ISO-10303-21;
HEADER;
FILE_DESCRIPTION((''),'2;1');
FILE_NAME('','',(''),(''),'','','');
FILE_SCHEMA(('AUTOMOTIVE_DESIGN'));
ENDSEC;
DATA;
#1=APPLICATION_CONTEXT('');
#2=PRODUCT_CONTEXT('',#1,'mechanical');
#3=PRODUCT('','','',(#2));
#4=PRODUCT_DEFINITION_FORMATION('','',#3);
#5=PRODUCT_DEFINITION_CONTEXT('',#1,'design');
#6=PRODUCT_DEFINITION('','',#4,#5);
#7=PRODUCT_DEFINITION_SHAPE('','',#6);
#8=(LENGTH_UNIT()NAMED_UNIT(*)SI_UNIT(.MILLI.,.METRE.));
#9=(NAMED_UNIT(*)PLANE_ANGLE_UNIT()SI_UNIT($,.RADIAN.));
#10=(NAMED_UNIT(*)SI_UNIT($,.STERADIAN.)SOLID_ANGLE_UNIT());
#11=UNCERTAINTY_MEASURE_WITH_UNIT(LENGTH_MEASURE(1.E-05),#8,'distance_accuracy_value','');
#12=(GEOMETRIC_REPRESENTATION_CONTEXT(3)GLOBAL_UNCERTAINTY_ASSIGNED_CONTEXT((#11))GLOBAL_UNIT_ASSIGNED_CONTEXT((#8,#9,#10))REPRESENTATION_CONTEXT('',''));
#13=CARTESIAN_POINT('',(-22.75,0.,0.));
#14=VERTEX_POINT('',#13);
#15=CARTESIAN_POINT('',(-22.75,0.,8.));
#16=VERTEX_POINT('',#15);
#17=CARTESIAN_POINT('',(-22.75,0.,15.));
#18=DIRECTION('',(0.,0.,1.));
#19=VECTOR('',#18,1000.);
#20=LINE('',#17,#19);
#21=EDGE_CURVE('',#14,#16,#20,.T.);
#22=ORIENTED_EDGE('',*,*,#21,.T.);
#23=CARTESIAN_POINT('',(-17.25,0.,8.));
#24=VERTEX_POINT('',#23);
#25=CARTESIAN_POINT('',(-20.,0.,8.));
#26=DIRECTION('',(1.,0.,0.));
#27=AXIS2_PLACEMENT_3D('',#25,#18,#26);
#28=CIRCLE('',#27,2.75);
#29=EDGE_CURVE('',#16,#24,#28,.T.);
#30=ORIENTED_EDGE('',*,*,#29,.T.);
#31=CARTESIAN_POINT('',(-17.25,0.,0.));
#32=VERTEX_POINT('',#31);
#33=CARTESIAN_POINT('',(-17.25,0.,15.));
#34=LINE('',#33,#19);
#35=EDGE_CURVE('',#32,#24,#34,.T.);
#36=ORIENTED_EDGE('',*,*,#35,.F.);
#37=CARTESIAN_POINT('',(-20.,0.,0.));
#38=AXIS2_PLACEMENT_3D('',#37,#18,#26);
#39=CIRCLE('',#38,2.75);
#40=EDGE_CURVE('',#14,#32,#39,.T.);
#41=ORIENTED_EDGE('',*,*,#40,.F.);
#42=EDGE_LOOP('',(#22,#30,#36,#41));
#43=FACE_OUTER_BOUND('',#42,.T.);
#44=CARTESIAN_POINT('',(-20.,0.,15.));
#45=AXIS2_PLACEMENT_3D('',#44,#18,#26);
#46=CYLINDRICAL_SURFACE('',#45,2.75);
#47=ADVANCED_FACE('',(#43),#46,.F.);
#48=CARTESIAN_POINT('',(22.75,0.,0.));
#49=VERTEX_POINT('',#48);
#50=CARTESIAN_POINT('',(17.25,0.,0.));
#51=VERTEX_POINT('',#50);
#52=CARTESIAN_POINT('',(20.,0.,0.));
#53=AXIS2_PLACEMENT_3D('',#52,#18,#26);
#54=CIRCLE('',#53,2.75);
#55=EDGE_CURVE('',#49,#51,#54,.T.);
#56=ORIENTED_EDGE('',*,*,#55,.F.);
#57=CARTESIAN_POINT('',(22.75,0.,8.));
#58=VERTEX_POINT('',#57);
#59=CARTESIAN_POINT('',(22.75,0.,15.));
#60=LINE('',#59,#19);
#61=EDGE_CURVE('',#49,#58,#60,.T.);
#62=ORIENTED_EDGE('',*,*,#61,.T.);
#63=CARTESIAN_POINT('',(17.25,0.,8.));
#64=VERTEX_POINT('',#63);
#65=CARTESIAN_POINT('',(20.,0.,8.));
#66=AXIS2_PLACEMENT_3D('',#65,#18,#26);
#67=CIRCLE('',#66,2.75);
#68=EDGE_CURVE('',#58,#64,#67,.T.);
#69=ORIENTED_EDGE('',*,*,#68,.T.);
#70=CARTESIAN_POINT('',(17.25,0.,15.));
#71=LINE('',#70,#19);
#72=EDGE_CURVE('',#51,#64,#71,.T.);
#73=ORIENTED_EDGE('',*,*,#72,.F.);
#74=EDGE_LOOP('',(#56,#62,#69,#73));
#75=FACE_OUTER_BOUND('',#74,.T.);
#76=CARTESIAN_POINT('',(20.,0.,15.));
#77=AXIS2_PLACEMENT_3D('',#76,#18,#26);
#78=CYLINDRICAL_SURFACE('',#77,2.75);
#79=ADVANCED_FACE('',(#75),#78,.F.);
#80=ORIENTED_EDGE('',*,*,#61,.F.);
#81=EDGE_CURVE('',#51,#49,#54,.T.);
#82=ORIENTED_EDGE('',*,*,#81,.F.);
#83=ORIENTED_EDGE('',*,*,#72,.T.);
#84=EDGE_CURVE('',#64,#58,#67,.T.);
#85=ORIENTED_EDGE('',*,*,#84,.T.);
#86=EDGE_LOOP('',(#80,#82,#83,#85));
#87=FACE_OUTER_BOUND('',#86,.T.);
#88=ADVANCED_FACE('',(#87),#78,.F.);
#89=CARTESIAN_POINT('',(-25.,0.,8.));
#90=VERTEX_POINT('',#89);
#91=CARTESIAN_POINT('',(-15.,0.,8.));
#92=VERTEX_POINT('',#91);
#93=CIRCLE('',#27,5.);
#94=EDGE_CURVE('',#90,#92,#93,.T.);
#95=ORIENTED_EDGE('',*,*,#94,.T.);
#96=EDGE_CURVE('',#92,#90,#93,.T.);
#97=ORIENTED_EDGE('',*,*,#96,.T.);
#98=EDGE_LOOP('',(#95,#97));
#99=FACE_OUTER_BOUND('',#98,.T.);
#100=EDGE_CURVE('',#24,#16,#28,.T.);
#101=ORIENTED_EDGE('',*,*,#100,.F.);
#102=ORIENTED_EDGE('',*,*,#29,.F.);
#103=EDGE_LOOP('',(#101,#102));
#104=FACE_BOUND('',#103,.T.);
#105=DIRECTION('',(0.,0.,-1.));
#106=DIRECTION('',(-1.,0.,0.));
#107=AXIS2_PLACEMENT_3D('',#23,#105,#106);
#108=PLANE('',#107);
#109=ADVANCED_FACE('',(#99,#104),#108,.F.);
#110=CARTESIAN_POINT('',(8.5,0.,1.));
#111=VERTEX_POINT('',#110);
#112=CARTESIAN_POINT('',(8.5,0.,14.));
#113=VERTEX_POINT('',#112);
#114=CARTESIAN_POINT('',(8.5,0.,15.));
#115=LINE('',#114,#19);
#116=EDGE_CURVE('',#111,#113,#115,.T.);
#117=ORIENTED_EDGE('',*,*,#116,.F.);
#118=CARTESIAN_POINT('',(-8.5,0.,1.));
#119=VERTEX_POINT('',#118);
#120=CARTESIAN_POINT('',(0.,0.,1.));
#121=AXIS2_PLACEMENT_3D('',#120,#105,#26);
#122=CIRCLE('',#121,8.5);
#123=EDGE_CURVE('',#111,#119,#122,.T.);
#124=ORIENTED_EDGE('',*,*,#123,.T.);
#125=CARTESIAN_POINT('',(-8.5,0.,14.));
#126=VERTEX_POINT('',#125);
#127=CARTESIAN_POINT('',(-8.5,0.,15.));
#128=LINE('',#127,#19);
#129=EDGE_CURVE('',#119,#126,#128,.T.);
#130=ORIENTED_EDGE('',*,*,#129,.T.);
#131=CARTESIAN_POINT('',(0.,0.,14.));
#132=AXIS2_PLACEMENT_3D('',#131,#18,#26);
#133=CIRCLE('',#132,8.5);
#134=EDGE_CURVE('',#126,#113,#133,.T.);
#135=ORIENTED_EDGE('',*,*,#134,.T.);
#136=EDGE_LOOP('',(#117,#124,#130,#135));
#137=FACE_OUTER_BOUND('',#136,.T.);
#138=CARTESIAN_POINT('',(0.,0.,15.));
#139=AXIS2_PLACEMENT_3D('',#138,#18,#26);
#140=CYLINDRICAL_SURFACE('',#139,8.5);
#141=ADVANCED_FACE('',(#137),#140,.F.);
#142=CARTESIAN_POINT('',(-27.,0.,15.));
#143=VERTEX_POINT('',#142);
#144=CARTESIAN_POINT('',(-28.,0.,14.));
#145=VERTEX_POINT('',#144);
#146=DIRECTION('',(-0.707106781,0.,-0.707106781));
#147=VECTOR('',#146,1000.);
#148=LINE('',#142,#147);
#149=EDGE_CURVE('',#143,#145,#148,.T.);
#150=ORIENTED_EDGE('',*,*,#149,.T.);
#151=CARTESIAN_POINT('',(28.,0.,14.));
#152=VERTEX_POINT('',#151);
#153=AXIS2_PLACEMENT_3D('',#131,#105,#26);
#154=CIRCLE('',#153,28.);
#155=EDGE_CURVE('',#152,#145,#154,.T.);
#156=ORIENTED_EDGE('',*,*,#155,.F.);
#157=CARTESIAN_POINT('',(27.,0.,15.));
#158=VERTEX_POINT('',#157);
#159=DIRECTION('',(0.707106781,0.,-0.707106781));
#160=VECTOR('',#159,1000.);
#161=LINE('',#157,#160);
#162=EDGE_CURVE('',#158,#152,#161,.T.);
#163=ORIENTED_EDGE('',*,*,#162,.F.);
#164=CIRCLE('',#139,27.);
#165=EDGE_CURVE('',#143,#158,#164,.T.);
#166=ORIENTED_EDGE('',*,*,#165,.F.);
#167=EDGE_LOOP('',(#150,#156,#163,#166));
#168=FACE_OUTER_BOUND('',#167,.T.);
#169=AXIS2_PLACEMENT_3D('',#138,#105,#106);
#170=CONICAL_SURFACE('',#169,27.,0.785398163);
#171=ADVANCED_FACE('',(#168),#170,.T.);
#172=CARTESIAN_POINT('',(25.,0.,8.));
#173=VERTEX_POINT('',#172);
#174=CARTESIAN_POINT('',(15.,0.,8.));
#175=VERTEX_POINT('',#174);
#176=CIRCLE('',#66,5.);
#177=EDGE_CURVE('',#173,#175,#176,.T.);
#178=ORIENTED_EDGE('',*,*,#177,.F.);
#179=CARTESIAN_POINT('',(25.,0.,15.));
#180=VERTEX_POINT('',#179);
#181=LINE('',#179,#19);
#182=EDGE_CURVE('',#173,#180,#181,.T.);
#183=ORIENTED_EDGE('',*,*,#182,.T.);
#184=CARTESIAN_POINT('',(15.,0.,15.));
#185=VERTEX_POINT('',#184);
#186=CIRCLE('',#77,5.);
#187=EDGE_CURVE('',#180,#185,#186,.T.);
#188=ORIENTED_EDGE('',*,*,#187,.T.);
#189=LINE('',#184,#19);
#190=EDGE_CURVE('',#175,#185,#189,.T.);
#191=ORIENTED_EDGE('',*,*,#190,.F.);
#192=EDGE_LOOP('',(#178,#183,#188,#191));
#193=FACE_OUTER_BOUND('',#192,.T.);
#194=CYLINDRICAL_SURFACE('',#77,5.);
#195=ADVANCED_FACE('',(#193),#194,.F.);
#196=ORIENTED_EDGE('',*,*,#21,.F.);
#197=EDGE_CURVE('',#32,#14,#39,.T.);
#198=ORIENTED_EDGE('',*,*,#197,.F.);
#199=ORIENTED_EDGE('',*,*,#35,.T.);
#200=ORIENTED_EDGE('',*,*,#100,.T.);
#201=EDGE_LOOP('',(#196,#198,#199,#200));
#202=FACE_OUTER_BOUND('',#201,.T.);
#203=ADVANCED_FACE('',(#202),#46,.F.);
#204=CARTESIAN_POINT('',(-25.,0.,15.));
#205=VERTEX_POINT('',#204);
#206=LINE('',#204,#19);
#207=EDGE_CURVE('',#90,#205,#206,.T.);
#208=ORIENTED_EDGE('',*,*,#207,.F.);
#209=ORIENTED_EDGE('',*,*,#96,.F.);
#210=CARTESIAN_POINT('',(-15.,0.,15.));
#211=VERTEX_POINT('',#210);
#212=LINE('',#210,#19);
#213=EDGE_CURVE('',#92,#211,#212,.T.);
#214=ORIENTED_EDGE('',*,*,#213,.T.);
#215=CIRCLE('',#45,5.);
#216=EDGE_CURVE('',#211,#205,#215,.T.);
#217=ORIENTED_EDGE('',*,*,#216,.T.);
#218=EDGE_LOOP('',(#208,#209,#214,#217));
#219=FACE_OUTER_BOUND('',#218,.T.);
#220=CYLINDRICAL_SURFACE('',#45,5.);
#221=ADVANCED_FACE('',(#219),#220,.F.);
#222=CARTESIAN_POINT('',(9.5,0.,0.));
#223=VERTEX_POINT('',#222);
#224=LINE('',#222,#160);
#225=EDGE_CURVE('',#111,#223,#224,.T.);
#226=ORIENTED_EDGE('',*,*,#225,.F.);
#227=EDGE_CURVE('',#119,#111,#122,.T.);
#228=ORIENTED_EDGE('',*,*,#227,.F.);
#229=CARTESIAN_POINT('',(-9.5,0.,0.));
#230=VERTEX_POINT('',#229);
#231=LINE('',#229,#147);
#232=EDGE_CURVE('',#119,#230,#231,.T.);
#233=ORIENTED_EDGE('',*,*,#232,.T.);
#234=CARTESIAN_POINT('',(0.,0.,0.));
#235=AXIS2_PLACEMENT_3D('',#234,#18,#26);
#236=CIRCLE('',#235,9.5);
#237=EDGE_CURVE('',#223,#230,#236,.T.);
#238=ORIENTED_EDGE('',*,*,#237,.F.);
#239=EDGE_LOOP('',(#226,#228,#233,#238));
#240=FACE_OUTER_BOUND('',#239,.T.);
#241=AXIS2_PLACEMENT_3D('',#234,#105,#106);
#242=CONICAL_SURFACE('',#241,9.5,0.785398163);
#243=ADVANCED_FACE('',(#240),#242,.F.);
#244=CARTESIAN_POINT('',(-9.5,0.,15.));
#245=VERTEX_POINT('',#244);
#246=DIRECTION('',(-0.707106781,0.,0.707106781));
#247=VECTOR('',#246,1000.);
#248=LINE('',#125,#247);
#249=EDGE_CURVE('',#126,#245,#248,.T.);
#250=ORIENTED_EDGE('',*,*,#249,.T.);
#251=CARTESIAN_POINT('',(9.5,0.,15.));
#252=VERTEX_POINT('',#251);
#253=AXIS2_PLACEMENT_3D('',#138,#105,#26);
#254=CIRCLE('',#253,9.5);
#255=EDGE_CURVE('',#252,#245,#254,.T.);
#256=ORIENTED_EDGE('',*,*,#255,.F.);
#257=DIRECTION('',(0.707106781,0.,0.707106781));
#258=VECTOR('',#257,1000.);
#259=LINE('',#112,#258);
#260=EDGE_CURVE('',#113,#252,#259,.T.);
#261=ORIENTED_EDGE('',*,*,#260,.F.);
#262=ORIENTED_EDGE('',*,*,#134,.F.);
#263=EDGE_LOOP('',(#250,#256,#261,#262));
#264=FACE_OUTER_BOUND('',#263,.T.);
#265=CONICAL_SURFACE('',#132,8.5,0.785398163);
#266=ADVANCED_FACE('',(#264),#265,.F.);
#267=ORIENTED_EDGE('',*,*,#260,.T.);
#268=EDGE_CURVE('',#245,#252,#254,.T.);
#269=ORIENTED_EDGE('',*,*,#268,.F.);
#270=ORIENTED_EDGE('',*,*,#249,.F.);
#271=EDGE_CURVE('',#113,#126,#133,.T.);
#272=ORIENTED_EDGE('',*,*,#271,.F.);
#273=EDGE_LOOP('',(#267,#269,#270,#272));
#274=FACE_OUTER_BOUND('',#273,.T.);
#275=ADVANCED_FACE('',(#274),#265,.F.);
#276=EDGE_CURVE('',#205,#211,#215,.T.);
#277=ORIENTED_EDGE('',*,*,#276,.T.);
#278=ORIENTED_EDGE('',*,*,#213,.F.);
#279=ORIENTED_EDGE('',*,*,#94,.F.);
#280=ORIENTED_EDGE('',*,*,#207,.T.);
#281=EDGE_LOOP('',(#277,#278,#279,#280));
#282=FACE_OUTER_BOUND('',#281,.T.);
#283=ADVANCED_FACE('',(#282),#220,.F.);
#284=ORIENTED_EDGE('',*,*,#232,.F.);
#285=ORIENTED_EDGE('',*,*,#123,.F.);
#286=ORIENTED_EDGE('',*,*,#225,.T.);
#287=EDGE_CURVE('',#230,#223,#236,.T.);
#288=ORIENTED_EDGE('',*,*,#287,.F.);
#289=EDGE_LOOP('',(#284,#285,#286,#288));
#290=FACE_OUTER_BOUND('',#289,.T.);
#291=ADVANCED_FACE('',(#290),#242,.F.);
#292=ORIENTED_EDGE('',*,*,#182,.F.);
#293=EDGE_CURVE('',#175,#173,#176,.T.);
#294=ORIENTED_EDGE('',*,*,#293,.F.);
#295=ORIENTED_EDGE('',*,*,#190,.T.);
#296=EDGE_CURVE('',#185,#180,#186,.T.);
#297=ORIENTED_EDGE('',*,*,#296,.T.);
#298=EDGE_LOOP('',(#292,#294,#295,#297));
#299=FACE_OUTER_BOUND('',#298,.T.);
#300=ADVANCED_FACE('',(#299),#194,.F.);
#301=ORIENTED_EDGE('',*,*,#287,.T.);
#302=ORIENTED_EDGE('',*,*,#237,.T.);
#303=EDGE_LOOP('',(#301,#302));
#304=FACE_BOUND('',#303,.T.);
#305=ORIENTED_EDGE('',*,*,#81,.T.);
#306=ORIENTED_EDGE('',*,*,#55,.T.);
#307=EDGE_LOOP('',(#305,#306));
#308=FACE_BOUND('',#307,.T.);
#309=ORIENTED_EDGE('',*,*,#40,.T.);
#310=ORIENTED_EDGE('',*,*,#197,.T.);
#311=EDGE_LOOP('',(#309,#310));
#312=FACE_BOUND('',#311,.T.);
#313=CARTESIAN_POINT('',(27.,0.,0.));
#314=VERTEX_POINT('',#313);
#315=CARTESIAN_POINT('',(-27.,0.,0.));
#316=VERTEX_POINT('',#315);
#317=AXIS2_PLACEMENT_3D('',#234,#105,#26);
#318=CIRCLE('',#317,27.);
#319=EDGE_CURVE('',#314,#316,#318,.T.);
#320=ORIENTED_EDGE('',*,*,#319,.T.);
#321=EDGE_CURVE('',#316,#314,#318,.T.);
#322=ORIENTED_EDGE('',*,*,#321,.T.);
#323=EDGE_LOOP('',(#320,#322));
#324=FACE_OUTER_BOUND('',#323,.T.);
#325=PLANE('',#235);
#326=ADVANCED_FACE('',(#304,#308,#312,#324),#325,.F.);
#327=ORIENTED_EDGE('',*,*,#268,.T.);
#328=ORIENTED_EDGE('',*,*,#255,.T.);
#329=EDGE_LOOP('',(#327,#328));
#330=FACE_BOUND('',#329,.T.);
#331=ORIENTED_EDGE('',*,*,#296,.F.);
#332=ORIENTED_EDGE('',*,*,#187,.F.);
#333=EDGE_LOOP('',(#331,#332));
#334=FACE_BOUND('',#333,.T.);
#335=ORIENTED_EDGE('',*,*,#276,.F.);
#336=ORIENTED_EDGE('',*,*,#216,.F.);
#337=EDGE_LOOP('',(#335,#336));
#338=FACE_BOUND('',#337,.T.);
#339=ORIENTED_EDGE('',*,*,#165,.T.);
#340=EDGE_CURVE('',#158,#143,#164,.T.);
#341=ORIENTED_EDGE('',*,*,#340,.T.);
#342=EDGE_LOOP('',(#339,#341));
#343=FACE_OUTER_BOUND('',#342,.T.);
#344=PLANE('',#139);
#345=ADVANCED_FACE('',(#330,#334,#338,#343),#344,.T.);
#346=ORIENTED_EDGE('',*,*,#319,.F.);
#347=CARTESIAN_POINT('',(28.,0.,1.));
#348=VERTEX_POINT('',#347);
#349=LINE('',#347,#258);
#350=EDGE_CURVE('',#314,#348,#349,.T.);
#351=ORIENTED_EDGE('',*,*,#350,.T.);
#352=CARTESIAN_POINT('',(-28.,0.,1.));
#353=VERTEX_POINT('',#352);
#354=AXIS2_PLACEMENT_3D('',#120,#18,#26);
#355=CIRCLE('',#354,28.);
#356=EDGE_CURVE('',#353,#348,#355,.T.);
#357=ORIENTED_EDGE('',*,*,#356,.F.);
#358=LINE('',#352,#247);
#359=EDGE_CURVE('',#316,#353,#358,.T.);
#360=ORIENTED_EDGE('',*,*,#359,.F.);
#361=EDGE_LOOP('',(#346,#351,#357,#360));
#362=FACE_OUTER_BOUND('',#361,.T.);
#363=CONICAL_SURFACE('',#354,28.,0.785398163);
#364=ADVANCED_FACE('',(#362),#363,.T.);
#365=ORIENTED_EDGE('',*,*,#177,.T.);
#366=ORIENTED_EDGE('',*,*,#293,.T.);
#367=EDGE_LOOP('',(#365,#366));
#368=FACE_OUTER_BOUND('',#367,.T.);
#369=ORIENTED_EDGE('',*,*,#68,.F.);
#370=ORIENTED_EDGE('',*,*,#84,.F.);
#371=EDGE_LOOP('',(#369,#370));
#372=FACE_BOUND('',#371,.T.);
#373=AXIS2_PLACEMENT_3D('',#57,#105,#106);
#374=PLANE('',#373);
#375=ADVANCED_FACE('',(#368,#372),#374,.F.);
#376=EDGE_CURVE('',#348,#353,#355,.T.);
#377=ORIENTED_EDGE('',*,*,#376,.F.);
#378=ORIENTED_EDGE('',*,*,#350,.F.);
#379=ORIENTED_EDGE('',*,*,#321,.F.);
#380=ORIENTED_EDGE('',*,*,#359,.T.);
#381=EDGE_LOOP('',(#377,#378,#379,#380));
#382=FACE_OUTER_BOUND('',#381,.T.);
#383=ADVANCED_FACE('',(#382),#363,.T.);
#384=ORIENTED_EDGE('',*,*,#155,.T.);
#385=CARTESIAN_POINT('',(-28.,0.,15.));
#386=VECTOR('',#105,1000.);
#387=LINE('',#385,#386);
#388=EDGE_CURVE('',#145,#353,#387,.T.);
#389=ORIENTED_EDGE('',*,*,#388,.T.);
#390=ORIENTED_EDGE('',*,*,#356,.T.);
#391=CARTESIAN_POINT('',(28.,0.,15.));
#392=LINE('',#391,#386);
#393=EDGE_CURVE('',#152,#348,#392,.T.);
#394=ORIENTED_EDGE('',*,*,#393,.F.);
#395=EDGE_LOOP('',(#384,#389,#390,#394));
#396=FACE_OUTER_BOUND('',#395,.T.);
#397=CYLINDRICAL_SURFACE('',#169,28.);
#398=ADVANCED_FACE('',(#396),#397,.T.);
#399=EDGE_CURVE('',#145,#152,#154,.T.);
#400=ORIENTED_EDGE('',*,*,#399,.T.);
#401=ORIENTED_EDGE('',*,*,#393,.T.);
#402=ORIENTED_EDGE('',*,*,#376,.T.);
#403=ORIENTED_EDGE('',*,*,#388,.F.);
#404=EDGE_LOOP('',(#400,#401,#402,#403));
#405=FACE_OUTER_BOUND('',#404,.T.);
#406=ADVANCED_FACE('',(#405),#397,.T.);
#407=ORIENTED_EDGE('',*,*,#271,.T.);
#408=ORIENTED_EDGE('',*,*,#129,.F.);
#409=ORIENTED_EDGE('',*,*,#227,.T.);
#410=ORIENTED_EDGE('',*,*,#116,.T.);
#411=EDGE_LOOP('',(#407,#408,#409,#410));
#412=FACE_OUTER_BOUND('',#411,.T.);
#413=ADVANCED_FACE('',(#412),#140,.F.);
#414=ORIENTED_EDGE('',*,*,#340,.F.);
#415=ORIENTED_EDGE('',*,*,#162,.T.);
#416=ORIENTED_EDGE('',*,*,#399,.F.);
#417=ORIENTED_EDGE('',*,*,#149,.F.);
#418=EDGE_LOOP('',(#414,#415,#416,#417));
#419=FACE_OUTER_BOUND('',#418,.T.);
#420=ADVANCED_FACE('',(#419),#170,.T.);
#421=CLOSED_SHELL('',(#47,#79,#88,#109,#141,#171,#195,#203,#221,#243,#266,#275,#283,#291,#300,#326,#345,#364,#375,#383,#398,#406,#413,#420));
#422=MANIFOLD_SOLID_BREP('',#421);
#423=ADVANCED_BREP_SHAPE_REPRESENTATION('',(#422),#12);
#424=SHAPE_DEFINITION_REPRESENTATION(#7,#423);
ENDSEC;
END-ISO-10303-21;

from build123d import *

# Parameters (mm, degrees)
SKETCH1_R           = 28
BOSS_EXTRUDE1_DEPTH = 15
HOLE1_D             = 17
HOLE2_D             = 5.5
HOLE2_CBORE_D       = 10
HOLE2_CBORE_DEPTH   = 7
CHAMFER1_SIZE       = 1


with BuildPart() as part:
    # Sketch1 → Boss-Extrude1 (new body)
    with BuildSketch(Plane.XY):
        Circle(SKETCH1_R)
    extrude(amount=BOSS_EXTRUDE1_DEPTH)

    # Hole1 (through all)
    with Locations(Plane.XY.offset(15)):
        with Locations((0, 0)):
            Hole(HOLE1_D / 2)

    # Hole2 (through all)
    with Locations(Plane.XY.offset(15)):
        with Locations((-20, 0), (20, 0)):
            CounterBoreHole(HOLE2_D / 2, HOLE2_CBORE_D / 2, HOLE2_CBORE_DEPTH)

    # Chamfer1
    chamfer1_edges = [part.edges().sort_by_distance(p)[0] for p in [
        (-28, 0, 0),
        (-28, 0, 15),
        (8.5, 0, 15),
        (8.5, 0, 0),
    ]]
    chamfer(chamfer1_edges, length=CHAMFER1_SIZE)


solid = part.part
